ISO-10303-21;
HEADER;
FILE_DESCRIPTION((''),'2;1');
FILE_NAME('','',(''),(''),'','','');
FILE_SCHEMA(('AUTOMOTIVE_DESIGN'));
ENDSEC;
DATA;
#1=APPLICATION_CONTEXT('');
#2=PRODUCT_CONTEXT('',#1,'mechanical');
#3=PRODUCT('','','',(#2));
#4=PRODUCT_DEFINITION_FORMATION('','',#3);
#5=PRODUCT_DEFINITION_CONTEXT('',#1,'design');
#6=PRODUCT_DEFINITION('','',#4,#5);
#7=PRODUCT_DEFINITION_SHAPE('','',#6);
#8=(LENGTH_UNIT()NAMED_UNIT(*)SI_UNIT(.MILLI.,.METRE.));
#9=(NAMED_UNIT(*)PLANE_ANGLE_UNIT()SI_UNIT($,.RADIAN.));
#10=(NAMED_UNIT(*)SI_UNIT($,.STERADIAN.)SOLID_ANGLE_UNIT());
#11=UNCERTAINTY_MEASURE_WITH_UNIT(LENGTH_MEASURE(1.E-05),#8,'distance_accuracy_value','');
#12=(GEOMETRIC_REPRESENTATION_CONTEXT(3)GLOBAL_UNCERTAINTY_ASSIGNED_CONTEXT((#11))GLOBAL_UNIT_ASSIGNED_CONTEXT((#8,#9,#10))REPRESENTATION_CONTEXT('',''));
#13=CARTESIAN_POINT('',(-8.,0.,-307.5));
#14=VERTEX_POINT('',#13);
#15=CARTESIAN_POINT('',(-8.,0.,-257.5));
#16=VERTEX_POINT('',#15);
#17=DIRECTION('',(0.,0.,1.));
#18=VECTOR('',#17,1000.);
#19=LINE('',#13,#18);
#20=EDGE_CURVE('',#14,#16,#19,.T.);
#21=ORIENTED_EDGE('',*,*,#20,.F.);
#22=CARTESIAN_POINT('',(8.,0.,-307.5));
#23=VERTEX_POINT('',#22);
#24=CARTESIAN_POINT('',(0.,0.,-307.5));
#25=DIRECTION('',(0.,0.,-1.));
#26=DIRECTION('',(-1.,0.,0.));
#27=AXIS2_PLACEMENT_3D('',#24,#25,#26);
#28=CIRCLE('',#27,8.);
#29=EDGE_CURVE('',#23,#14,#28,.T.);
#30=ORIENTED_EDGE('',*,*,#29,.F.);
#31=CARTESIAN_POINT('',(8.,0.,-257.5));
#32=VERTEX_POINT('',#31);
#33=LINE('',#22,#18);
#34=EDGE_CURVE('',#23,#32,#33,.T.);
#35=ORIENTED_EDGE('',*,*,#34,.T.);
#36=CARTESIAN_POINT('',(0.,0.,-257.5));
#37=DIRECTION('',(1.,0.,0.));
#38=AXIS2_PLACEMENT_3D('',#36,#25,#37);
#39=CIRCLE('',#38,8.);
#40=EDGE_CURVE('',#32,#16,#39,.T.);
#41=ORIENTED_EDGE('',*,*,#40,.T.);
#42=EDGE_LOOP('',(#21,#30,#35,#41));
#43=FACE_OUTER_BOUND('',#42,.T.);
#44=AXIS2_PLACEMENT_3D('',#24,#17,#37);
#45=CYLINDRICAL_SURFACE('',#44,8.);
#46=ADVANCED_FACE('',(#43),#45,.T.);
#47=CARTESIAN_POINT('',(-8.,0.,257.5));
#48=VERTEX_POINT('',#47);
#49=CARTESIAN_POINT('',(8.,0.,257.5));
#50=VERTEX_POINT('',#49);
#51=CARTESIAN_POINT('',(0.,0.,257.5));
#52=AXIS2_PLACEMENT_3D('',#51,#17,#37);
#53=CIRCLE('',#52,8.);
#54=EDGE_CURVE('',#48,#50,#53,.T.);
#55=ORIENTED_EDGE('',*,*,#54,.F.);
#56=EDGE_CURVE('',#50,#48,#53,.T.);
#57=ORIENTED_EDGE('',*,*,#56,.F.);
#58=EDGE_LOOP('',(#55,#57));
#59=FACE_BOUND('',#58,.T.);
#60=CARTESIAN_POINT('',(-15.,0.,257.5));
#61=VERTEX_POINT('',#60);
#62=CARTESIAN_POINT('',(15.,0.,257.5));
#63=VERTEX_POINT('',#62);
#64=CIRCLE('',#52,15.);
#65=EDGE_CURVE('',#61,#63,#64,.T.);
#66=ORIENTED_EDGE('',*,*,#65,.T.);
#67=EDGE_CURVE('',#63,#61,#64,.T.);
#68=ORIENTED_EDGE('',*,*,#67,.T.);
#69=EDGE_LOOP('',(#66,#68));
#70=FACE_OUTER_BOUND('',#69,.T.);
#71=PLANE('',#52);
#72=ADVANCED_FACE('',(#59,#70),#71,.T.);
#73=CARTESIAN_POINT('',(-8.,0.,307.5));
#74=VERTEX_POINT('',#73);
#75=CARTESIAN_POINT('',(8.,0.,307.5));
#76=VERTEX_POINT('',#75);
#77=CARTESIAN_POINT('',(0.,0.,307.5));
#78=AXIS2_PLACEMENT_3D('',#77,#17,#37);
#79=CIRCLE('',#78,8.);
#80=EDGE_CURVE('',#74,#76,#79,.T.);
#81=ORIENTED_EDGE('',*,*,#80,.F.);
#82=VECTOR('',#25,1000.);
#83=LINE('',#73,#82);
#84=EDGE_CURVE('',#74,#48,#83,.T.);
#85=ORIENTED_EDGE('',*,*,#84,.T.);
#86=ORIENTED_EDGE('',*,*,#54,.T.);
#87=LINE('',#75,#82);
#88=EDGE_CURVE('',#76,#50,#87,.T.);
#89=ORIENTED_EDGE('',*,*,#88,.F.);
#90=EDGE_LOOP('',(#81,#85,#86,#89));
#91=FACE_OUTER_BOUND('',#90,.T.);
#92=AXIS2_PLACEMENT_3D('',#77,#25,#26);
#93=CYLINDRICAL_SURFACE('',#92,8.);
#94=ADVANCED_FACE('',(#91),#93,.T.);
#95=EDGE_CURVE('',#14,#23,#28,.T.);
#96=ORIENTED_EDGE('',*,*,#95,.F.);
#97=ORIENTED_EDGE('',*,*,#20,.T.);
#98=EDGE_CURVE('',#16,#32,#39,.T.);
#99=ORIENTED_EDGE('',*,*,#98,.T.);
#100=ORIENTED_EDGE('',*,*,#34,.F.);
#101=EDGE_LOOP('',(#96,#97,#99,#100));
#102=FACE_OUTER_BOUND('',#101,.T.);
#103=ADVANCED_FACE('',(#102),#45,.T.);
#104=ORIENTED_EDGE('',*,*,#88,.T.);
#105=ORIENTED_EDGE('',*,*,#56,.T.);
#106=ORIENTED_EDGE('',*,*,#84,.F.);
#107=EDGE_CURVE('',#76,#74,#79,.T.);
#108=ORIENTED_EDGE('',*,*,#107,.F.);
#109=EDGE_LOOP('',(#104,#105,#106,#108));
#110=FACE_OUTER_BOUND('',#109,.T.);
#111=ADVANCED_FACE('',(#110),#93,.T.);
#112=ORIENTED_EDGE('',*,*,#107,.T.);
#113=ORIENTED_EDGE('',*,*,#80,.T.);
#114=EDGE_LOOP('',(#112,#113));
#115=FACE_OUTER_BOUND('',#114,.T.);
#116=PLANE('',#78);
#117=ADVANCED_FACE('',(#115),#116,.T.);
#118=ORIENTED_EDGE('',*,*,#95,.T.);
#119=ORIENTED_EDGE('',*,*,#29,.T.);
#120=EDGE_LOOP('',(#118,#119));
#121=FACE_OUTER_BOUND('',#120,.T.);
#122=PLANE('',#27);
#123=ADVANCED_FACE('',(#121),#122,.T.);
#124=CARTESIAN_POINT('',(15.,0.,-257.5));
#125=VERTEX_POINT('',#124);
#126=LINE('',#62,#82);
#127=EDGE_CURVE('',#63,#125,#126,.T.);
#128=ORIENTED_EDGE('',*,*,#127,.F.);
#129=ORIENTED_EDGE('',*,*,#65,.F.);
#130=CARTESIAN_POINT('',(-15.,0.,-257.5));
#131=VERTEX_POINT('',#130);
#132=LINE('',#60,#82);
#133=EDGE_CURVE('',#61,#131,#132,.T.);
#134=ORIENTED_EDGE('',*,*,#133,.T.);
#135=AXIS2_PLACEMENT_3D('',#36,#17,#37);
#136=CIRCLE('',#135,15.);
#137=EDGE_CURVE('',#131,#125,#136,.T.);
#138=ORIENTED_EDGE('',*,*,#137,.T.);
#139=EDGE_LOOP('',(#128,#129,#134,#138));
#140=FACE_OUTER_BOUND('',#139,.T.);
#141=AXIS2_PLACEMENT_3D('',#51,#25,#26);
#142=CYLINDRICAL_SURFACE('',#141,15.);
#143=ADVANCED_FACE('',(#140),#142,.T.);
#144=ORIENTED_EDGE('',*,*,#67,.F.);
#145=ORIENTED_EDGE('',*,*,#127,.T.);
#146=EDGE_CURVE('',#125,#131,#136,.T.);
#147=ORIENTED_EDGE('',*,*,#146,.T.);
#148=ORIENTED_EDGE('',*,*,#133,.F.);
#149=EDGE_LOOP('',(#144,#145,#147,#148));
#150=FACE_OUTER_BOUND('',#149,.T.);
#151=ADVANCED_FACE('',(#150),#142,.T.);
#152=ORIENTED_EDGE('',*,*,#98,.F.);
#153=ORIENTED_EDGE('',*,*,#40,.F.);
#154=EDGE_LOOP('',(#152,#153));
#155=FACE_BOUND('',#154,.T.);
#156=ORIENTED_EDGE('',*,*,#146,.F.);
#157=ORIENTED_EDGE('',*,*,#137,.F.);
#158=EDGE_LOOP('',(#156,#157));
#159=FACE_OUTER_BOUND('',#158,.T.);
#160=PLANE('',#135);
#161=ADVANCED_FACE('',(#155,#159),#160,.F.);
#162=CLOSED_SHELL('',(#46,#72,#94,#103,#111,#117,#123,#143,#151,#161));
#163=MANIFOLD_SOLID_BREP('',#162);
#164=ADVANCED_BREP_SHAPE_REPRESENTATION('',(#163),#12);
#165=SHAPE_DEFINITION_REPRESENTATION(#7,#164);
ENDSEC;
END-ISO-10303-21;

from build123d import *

# Parameters (mm, degrees)
SKETCH1_R           = 15
BOSS_EXTRUDE1_DEPTH = 257.5
SKETCH2_R           = 8
BOSS_EXTRUDE2_DEPTH = 50
BOSS_EXTRUDE3_START = 50
SKETCH3_R           = 8
BOSS_EXTRUDE3_DEPTH = 50


with BuildPart() as part:
    # Sketch1 → Boss-Extrude1 (new, symmetric)
    with BuildSketch(Plane.XY):
        Circle(SKETCH1_R)
    extrude(amount=BOSS_EXTRUDE1_DEPTH, both=True)

    # Sketch2 → Boss-Extrude2 (add)
    with BuildSketch(Plane.XY.offset(257.5)):
        Circle(SKETCH2_R)
    extrude(amount=BOSS_EXTRUDE2_DEPTH)

    # Sketch3 → Boss-Extrude3 (add)
    with BuildSketch(Plane(origin=(0, 0, -257.5), x_dir=(-1, 0, 0), z_dir=(0, 0, -1)).offset(BOSS_EXTRUDE3_START)):
        with Locations(Location((0, 0, 0), (0, 0, 180))):
            Circle(SKETCH3_R)
    extrude(amount=-BOSS_EXTRUDE3_DEPTH)


solid = part.part
